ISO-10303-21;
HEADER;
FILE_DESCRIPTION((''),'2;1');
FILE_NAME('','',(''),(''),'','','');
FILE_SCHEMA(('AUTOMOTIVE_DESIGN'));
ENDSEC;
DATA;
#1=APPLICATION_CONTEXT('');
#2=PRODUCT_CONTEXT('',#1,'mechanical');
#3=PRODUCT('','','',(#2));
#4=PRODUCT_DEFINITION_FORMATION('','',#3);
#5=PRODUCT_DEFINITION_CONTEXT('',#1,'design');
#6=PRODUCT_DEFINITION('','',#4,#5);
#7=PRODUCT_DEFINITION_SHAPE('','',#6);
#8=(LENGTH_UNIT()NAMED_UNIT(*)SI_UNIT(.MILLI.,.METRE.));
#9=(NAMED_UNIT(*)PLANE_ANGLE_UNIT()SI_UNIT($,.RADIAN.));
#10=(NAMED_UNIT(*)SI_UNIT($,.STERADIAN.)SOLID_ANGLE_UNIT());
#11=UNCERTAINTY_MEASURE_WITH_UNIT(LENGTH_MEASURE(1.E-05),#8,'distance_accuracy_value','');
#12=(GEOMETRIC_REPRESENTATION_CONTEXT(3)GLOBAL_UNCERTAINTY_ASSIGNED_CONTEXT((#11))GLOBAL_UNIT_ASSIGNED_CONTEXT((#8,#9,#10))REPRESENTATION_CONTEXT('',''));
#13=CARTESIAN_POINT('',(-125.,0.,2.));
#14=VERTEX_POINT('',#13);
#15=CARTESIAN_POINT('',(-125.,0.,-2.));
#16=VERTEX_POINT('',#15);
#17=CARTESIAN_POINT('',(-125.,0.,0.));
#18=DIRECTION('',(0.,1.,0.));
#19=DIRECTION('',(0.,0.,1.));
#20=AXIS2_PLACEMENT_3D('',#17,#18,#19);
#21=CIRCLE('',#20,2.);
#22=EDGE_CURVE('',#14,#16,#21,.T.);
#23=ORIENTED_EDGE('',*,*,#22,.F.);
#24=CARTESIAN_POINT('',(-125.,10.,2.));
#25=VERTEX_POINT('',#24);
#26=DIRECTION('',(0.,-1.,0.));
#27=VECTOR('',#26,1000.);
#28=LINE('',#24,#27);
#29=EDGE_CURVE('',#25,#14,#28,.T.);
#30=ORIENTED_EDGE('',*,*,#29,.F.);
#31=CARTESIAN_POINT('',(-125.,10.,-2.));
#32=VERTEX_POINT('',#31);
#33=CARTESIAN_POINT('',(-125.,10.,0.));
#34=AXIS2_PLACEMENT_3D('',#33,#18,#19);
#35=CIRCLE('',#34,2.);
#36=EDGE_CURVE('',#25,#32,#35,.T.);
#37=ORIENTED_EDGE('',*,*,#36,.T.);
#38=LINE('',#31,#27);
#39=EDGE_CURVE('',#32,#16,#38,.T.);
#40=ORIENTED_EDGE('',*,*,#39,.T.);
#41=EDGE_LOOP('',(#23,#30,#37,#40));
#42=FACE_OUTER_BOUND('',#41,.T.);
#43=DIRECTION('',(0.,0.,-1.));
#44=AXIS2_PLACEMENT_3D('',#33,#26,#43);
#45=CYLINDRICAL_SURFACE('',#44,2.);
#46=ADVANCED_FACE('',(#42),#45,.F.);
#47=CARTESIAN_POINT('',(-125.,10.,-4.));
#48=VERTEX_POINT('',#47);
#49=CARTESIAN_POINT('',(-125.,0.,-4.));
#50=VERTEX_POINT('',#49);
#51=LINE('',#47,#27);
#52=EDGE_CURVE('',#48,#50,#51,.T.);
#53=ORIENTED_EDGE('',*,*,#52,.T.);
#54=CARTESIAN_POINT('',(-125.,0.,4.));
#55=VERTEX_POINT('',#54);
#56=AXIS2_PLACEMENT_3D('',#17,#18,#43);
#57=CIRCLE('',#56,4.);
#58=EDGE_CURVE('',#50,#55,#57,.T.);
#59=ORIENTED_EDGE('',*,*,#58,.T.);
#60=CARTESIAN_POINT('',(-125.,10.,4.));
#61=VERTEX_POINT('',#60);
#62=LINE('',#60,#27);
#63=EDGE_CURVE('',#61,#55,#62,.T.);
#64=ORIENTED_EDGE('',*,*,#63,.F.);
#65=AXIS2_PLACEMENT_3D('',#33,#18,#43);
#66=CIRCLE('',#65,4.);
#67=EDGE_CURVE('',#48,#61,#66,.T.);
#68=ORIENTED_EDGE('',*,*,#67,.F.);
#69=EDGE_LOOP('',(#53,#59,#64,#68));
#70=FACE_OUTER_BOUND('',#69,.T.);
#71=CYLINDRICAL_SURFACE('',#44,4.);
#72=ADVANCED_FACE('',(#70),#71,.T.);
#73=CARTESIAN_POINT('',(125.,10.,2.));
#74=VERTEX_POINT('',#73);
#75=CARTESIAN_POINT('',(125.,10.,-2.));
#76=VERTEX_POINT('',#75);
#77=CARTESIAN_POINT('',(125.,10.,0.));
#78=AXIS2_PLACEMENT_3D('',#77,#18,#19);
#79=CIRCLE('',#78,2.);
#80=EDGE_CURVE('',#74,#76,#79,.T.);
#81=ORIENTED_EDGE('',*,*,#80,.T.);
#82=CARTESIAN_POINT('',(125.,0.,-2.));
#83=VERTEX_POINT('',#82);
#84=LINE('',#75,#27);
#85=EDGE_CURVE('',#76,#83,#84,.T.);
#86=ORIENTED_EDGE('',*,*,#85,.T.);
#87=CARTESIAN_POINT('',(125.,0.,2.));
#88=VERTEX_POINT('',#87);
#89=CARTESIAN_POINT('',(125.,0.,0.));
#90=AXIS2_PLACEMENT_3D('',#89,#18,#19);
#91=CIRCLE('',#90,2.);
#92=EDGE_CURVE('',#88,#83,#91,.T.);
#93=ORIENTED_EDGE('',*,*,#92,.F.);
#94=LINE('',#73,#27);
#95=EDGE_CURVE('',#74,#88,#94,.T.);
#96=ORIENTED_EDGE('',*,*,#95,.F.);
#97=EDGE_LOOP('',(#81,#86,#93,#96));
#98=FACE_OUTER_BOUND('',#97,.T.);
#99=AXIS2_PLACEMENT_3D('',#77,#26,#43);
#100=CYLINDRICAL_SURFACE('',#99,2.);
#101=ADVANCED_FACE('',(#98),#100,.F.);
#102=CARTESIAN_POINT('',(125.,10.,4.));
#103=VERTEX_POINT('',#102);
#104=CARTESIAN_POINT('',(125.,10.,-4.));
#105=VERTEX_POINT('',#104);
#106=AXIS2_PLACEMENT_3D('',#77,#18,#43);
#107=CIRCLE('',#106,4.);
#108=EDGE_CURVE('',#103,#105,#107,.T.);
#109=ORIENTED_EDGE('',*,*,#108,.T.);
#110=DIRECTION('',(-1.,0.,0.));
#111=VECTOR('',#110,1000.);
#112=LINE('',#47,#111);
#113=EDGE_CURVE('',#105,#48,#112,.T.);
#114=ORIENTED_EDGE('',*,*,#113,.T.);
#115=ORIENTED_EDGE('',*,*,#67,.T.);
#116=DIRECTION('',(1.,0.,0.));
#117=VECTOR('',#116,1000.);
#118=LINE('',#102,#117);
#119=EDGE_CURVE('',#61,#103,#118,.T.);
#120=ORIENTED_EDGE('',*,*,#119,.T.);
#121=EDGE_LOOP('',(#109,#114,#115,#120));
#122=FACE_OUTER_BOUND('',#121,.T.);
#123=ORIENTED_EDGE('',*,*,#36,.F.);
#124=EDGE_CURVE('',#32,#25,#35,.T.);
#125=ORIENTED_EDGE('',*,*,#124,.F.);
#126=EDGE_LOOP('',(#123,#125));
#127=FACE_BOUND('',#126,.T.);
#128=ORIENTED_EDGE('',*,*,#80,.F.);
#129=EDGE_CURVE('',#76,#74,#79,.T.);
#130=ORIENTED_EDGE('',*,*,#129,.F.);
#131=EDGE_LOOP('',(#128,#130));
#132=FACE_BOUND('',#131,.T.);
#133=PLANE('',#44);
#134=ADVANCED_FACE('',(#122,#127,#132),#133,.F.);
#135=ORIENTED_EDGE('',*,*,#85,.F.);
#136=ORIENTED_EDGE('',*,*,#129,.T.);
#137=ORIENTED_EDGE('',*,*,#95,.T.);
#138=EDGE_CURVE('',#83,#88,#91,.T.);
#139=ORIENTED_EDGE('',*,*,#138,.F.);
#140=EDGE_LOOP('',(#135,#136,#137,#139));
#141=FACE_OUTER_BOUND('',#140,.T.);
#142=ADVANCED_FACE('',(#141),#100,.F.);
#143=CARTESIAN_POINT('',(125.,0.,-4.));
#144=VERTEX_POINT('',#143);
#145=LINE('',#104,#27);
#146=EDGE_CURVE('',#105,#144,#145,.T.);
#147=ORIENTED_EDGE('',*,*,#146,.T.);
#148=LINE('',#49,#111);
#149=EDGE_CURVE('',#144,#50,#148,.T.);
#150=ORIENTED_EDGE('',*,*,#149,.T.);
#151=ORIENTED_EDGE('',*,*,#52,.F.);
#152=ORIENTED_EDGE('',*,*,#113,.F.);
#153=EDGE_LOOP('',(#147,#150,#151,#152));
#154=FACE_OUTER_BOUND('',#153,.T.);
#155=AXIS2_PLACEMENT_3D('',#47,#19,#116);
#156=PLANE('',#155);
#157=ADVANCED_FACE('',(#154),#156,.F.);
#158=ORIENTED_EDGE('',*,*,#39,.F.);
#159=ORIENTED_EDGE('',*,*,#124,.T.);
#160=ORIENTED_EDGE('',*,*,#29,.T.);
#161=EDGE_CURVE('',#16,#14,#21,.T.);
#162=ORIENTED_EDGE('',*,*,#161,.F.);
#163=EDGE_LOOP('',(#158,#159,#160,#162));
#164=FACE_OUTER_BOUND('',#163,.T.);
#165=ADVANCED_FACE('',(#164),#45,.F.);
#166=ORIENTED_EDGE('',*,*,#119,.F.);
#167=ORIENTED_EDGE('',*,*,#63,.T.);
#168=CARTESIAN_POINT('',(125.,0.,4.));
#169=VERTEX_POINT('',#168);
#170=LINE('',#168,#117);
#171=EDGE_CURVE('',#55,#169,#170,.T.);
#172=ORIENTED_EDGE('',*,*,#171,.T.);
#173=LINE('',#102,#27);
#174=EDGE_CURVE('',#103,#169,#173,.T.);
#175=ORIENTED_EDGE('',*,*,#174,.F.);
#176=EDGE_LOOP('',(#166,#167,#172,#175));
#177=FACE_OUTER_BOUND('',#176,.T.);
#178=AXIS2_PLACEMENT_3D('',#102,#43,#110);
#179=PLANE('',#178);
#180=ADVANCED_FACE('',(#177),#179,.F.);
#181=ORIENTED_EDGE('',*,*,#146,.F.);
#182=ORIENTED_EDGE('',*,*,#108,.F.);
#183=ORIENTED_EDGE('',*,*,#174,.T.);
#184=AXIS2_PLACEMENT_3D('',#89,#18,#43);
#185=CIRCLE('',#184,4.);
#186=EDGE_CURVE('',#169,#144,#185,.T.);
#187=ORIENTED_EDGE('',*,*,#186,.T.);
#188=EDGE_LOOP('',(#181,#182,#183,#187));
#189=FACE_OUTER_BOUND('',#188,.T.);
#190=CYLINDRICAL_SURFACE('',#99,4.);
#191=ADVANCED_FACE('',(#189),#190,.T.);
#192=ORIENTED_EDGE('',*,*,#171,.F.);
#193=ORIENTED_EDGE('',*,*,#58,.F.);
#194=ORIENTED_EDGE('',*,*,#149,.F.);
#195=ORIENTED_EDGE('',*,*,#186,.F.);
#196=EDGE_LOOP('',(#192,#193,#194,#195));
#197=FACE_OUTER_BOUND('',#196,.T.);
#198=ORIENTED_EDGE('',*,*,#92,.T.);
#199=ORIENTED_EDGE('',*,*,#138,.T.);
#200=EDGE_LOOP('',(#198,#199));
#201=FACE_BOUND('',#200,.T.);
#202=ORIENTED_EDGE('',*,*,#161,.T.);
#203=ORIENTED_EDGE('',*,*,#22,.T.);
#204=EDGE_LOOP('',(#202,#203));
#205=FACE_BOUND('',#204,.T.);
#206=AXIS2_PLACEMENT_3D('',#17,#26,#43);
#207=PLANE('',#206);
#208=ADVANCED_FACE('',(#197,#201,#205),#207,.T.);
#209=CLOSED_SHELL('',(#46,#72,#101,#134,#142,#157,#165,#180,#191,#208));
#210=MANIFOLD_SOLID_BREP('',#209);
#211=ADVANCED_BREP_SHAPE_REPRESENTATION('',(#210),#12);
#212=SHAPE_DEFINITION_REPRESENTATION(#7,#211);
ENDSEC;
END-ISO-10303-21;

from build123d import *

# Parameters (mm, degrees)
SKETCH1_R           = 2
BOSS_EXTRUDE1_DEPTH = 10


with BuildPart() as part:
    # Sketch1 → Boss-Extrude1 (new body)
    with BuildSketch(Plane(origin=(0, 0, 0), x_dir=(1, 0, 0), z_dir=(0, 1, 0))):
        with BuildLine():
            Line((-125, 4), (125, 4))
            ThreePointArc((125, 4), (129, 0), (125, -4))
            Line((125, -4), (-125, -4))
            ThreePointArc((-125, -4), (-129, 0), (-125, 4))
        make_face()
        with Locations(Location((-125, 0, 0), (0, 0, 270))):
            Circle(SKETCH1_R, mode=Mode.SUBTRACT)
        with Locations(Location((125, 0, 0), (0, 0, 270))):
            Circle(SKETCH1_R, mode=Mode.SUBTRACT)
    extrude(amount=BOSS_EXTRUDE1_DEPTH)


solid = part.part
